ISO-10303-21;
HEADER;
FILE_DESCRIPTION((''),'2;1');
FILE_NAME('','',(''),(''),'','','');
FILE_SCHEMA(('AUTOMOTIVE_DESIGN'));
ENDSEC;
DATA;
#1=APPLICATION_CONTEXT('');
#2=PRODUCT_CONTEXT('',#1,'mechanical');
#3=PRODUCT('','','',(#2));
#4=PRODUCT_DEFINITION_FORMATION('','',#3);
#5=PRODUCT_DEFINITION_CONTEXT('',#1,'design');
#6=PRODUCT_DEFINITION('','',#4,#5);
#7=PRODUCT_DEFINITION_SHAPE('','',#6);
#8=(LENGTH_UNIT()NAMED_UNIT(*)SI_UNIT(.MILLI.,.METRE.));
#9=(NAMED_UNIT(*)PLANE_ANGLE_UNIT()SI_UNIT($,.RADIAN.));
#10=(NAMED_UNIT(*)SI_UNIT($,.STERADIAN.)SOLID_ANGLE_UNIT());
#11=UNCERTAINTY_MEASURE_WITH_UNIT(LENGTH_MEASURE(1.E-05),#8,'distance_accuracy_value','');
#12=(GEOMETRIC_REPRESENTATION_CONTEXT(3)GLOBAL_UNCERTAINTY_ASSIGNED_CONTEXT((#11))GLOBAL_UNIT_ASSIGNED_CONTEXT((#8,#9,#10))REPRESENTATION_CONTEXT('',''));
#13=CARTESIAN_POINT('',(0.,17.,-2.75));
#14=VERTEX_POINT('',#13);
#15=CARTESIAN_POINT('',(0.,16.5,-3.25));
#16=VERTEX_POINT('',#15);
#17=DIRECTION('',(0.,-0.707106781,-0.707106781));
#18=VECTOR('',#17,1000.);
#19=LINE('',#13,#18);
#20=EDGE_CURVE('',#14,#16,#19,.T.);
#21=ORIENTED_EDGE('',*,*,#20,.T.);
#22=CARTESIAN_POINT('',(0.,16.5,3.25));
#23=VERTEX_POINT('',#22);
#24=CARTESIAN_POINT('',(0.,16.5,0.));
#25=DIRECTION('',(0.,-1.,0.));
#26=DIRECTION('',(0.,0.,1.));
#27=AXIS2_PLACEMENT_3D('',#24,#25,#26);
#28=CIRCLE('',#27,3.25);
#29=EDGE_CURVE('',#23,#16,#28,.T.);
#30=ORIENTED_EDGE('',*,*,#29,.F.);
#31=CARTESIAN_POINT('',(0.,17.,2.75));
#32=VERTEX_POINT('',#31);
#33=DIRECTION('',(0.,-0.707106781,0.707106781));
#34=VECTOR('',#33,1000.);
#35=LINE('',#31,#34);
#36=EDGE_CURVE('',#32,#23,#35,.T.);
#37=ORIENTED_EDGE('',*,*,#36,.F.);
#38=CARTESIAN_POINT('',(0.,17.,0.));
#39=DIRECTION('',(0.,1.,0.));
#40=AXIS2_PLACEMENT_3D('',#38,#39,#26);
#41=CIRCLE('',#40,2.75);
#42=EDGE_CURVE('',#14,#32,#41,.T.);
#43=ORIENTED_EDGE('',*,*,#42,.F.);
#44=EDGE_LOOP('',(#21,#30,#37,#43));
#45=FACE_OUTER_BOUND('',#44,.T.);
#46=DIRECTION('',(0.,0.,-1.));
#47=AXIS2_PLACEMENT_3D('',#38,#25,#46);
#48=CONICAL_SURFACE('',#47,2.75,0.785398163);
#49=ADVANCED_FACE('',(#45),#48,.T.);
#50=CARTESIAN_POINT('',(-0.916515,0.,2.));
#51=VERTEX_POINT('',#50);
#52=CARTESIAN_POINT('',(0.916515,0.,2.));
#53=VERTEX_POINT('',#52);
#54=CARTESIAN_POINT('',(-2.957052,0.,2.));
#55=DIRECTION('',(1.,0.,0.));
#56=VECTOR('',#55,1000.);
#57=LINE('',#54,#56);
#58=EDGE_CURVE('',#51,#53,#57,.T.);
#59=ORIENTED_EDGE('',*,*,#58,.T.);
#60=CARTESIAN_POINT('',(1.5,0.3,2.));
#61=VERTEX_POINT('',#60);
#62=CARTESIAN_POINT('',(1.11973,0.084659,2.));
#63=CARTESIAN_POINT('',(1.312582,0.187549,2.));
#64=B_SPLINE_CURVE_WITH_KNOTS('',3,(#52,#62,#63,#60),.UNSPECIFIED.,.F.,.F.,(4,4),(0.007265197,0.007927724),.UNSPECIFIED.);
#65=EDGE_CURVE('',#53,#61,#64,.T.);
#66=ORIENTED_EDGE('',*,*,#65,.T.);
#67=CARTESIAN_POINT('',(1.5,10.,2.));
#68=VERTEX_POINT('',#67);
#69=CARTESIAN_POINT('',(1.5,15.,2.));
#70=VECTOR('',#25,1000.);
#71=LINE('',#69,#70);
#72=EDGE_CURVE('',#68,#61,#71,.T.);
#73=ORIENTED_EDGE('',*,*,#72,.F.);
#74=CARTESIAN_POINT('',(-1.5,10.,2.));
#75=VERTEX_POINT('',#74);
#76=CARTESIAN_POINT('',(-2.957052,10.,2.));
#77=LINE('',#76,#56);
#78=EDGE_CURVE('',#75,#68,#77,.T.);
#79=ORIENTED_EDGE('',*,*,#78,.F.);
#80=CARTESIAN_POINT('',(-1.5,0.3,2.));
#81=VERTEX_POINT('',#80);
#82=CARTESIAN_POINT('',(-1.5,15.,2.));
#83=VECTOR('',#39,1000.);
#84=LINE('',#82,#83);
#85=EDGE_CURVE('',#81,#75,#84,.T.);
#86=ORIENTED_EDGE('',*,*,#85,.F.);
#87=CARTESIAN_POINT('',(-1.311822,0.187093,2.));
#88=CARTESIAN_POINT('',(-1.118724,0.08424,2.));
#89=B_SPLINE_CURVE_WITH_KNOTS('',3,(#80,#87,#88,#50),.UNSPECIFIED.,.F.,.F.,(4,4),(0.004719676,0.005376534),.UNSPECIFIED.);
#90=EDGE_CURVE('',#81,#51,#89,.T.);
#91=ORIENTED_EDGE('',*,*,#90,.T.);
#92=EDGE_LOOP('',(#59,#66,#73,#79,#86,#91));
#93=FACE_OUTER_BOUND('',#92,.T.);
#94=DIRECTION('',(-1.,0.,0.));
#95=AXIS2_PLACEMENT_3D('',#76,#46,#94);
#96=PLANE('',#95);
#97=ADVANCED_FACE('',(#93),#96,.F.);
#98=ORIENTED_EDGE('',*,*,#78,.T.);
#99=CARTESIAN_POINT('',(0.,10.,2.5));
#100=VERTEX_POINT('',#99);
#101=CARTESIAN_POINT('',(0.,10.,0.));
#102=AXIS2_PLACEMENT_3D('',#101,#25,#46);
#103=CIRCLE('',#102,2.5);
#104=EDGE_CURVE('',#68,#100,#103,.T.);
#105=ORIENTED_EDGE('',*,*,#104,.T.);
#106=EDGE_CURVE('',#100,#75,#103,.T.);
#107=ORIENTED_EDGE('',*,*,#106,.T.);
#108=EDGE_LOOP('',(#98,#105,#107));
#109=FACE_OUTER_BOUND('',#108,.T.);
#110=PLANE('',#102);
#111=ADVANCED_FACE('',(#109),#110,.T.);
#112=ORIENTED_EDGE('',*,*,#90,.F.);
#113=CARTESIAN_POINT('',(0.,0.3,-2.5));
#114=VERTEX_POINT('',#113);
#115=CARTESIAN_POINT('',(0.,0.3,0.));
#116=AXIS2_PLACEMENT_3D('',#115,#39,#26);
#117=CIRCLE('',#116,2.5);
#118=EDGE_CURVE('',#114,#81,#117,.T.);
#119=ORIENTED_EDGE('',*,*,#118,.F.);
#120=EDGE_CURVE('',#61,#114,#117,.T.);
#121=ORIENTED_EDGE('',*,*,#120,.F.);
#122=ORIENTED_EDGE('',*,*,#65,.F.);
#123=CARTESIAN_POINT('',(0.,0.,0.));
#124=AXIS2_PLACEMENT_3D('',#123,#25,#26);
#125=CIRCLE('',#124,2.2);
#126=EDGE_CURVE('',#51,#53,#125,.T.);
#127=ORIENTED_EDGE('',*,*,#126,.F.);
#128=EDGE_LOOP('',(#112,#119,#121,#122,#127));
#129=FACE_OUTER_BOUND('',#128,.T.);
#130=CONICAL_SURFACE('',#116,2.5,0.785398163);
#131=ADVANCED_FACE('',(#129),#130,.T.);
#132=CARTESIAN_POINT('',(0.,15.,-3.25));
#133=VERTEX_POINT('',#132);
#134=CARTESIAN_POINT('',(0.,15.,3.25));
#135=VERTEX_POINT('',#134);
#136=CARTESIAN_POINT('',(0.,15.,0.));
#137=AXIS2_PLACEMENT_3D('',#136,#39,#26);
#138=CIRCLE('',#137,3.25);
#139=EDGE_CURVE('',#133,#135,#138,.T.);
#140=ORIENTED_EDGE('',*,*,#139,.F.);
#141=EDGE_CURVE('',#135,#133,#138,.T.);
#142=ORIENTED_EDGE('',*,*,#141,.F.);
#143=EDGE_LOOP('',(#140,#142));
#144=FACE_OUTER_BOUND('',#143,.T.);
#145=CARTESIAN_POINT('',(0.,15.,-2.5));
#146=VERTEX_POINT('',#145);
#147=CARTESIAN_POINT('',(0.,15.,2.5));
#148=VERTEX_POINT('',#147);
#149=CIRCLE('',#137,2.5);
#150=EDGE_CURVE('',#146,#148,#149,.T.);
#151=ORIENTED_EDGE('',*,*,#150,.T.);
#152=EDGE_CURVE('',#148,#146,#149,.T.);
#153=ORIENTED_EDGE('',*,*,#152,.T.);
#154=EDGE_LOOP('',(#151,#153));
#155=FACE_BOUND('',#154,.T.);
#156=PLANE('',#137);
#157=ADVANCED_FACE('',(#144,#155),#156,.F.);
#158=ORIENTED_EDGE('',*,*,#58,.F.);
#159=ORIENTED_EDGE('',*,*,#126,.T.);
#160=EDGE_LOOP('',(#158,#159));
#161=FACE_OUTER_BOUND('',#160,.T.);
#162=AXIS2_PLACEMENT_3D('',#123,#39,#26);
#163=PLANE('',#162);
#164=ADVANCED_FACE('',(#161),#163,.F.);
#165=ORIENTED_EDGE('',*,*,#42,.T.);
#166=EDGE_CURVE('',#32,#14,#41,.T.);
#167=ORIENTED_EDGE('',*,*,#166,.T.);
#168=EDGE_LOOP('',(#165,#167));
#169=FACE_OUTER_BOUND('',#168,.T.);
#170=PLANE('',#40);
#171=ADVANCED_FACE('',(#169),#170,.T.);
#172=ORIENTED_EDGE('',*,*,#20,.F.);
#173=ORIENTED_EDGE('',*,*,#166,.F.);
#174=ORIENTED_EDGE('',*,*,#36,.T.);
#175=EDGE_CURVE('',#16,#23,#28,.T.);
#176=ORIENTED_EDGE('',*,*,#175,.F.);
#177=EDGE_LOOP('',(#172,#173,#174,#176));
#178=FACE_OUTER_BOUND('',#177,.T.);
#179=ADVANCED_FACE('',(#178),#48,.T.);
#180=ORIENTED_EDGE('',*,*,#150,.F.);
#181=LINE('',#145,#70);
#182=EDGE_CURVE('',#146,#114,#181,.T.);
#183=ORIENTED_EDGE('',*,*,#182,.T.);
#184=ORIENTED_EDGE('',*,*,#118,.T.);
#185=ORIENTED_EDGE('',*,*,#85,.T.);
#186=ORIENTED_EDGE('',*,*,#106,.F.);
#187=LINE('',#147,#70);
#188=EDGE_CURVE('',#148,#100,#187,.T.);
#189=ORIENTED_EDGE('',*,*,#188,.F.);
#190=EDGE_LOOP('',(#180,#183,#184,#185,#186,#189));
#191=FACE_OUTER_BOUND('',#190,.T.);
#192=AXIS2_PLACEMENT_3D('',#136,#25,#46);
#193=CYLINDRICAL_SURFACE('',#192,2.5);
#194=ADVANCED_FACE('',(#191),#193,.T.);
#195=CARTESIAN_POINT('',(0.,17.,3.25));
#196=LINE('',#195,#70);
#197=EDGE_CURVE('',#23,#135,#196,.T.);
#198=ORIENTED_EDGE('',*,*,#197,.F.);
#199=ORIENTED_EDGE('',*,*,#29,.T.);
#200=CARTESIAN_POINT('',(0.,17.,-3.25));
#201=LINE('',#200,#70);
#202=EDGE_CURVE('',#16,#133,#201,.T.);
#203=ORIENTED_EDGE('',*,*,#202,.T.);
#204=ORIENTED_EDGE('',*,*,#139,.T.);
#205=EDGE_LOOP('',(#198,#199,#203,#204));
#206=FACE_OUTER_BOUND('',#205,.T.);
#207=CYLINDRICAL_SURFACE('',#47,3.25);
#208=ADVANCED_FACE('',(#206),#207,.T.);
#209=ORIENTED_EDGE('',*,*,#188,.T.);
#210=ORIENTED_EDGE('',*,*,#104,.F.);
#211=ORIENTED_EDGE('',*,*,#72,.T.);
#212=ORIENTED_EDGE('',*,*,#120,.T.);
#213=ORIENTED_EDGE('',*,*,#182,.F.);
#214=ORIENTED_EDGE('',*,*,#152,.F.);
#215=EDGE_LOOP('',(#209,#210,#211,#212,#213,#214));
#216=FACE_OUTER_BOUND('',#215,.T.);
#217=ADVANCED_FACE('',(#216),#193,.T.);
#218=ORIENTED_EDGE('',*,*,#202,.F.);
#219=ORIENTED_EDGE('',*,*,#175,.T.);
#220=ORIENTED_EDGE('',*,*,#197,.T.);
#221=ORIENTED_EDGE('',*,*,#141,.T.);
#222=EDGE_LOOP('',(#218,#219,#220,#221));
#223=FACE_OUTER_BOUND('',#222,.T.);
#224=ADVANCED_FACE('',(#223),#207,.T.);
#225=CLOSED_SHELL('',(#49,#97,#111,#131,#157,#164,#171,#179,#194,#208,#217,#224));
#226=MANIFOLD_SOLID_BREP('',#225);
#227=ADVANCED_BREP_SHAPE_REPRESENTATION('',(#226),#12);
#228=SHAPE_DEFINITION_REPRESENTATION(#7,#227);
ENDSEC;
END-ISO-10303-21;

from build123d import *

# Parameters (mm, degrees)
SKETCH1_R           = 2.5
BOSS_EXTRUDE1_DEPTH = 15
SKETCH2_R           = 3.25
BOSS_EXTRUDE2_DEPTH = 2
CHAMFER1_SIZE       = 0.5
CHAMFER2_SIZE       = 0.3
SKETCH3_W           = 5.914103074
SKETCH3_H           = 1
CUT_EXTRUDE1_DEPTH  = 10


with BuildPart() as part:
    # Sketch1 → Boss-Extrude1 (new body)
    with BuildSketch(Plane(origin=(0, 0, 0), x_dir=(1, 0, 0), z_dir=(0, 1, 0))):
        with Locations(Location((0, 0, 0), (0, 0, 270))):
            Circle(SKETCH1_R)
    extrude(amount=BOSS_EXTRUDE1_DEPTH)

    # Sketch2 → Boss-Extrude2 (add)
    with BuildSketch(Plane(origin=(0, 15, 0), x_dir=(1, 0, 0), z_dir=(0, 1, 0))):
        with Locations(Location((0, 0, 0), (0, 0, 270))):
            Circle(SKETCH2_R)
    extrude(amount=BOSS_EXTRUDE2_DEPTH)

    # Chamfer1
    chamfer1_edges = [part.edges().sort_by_distance(p)[0] for p in [
        (0, 17, -3.25),
    ]]
    chamfer(chamfer1_edges, length=CHAMFER1_SIZE)

    # Chamfer2
    chamfer2_edges = [part.edges().sort_by_distance(p)[0] for p in [
        (0, 0, -2.5),
    ]]
    chamfer(chamfer2_edges, length=CHAMFER2_SIZE)

    # Sketch3 → Cut-Extrude1 (cut)
    with BuildSketch(Plane.XZ):
        with Locations((0, 2.5)):
            Rectangle(SKETCH3_W, SKETCH3_H)
    extrude(amount=-CUT_EXTRUDE1_DEPTH, mode=Mode.SUBTRACT)


solid = part.part
